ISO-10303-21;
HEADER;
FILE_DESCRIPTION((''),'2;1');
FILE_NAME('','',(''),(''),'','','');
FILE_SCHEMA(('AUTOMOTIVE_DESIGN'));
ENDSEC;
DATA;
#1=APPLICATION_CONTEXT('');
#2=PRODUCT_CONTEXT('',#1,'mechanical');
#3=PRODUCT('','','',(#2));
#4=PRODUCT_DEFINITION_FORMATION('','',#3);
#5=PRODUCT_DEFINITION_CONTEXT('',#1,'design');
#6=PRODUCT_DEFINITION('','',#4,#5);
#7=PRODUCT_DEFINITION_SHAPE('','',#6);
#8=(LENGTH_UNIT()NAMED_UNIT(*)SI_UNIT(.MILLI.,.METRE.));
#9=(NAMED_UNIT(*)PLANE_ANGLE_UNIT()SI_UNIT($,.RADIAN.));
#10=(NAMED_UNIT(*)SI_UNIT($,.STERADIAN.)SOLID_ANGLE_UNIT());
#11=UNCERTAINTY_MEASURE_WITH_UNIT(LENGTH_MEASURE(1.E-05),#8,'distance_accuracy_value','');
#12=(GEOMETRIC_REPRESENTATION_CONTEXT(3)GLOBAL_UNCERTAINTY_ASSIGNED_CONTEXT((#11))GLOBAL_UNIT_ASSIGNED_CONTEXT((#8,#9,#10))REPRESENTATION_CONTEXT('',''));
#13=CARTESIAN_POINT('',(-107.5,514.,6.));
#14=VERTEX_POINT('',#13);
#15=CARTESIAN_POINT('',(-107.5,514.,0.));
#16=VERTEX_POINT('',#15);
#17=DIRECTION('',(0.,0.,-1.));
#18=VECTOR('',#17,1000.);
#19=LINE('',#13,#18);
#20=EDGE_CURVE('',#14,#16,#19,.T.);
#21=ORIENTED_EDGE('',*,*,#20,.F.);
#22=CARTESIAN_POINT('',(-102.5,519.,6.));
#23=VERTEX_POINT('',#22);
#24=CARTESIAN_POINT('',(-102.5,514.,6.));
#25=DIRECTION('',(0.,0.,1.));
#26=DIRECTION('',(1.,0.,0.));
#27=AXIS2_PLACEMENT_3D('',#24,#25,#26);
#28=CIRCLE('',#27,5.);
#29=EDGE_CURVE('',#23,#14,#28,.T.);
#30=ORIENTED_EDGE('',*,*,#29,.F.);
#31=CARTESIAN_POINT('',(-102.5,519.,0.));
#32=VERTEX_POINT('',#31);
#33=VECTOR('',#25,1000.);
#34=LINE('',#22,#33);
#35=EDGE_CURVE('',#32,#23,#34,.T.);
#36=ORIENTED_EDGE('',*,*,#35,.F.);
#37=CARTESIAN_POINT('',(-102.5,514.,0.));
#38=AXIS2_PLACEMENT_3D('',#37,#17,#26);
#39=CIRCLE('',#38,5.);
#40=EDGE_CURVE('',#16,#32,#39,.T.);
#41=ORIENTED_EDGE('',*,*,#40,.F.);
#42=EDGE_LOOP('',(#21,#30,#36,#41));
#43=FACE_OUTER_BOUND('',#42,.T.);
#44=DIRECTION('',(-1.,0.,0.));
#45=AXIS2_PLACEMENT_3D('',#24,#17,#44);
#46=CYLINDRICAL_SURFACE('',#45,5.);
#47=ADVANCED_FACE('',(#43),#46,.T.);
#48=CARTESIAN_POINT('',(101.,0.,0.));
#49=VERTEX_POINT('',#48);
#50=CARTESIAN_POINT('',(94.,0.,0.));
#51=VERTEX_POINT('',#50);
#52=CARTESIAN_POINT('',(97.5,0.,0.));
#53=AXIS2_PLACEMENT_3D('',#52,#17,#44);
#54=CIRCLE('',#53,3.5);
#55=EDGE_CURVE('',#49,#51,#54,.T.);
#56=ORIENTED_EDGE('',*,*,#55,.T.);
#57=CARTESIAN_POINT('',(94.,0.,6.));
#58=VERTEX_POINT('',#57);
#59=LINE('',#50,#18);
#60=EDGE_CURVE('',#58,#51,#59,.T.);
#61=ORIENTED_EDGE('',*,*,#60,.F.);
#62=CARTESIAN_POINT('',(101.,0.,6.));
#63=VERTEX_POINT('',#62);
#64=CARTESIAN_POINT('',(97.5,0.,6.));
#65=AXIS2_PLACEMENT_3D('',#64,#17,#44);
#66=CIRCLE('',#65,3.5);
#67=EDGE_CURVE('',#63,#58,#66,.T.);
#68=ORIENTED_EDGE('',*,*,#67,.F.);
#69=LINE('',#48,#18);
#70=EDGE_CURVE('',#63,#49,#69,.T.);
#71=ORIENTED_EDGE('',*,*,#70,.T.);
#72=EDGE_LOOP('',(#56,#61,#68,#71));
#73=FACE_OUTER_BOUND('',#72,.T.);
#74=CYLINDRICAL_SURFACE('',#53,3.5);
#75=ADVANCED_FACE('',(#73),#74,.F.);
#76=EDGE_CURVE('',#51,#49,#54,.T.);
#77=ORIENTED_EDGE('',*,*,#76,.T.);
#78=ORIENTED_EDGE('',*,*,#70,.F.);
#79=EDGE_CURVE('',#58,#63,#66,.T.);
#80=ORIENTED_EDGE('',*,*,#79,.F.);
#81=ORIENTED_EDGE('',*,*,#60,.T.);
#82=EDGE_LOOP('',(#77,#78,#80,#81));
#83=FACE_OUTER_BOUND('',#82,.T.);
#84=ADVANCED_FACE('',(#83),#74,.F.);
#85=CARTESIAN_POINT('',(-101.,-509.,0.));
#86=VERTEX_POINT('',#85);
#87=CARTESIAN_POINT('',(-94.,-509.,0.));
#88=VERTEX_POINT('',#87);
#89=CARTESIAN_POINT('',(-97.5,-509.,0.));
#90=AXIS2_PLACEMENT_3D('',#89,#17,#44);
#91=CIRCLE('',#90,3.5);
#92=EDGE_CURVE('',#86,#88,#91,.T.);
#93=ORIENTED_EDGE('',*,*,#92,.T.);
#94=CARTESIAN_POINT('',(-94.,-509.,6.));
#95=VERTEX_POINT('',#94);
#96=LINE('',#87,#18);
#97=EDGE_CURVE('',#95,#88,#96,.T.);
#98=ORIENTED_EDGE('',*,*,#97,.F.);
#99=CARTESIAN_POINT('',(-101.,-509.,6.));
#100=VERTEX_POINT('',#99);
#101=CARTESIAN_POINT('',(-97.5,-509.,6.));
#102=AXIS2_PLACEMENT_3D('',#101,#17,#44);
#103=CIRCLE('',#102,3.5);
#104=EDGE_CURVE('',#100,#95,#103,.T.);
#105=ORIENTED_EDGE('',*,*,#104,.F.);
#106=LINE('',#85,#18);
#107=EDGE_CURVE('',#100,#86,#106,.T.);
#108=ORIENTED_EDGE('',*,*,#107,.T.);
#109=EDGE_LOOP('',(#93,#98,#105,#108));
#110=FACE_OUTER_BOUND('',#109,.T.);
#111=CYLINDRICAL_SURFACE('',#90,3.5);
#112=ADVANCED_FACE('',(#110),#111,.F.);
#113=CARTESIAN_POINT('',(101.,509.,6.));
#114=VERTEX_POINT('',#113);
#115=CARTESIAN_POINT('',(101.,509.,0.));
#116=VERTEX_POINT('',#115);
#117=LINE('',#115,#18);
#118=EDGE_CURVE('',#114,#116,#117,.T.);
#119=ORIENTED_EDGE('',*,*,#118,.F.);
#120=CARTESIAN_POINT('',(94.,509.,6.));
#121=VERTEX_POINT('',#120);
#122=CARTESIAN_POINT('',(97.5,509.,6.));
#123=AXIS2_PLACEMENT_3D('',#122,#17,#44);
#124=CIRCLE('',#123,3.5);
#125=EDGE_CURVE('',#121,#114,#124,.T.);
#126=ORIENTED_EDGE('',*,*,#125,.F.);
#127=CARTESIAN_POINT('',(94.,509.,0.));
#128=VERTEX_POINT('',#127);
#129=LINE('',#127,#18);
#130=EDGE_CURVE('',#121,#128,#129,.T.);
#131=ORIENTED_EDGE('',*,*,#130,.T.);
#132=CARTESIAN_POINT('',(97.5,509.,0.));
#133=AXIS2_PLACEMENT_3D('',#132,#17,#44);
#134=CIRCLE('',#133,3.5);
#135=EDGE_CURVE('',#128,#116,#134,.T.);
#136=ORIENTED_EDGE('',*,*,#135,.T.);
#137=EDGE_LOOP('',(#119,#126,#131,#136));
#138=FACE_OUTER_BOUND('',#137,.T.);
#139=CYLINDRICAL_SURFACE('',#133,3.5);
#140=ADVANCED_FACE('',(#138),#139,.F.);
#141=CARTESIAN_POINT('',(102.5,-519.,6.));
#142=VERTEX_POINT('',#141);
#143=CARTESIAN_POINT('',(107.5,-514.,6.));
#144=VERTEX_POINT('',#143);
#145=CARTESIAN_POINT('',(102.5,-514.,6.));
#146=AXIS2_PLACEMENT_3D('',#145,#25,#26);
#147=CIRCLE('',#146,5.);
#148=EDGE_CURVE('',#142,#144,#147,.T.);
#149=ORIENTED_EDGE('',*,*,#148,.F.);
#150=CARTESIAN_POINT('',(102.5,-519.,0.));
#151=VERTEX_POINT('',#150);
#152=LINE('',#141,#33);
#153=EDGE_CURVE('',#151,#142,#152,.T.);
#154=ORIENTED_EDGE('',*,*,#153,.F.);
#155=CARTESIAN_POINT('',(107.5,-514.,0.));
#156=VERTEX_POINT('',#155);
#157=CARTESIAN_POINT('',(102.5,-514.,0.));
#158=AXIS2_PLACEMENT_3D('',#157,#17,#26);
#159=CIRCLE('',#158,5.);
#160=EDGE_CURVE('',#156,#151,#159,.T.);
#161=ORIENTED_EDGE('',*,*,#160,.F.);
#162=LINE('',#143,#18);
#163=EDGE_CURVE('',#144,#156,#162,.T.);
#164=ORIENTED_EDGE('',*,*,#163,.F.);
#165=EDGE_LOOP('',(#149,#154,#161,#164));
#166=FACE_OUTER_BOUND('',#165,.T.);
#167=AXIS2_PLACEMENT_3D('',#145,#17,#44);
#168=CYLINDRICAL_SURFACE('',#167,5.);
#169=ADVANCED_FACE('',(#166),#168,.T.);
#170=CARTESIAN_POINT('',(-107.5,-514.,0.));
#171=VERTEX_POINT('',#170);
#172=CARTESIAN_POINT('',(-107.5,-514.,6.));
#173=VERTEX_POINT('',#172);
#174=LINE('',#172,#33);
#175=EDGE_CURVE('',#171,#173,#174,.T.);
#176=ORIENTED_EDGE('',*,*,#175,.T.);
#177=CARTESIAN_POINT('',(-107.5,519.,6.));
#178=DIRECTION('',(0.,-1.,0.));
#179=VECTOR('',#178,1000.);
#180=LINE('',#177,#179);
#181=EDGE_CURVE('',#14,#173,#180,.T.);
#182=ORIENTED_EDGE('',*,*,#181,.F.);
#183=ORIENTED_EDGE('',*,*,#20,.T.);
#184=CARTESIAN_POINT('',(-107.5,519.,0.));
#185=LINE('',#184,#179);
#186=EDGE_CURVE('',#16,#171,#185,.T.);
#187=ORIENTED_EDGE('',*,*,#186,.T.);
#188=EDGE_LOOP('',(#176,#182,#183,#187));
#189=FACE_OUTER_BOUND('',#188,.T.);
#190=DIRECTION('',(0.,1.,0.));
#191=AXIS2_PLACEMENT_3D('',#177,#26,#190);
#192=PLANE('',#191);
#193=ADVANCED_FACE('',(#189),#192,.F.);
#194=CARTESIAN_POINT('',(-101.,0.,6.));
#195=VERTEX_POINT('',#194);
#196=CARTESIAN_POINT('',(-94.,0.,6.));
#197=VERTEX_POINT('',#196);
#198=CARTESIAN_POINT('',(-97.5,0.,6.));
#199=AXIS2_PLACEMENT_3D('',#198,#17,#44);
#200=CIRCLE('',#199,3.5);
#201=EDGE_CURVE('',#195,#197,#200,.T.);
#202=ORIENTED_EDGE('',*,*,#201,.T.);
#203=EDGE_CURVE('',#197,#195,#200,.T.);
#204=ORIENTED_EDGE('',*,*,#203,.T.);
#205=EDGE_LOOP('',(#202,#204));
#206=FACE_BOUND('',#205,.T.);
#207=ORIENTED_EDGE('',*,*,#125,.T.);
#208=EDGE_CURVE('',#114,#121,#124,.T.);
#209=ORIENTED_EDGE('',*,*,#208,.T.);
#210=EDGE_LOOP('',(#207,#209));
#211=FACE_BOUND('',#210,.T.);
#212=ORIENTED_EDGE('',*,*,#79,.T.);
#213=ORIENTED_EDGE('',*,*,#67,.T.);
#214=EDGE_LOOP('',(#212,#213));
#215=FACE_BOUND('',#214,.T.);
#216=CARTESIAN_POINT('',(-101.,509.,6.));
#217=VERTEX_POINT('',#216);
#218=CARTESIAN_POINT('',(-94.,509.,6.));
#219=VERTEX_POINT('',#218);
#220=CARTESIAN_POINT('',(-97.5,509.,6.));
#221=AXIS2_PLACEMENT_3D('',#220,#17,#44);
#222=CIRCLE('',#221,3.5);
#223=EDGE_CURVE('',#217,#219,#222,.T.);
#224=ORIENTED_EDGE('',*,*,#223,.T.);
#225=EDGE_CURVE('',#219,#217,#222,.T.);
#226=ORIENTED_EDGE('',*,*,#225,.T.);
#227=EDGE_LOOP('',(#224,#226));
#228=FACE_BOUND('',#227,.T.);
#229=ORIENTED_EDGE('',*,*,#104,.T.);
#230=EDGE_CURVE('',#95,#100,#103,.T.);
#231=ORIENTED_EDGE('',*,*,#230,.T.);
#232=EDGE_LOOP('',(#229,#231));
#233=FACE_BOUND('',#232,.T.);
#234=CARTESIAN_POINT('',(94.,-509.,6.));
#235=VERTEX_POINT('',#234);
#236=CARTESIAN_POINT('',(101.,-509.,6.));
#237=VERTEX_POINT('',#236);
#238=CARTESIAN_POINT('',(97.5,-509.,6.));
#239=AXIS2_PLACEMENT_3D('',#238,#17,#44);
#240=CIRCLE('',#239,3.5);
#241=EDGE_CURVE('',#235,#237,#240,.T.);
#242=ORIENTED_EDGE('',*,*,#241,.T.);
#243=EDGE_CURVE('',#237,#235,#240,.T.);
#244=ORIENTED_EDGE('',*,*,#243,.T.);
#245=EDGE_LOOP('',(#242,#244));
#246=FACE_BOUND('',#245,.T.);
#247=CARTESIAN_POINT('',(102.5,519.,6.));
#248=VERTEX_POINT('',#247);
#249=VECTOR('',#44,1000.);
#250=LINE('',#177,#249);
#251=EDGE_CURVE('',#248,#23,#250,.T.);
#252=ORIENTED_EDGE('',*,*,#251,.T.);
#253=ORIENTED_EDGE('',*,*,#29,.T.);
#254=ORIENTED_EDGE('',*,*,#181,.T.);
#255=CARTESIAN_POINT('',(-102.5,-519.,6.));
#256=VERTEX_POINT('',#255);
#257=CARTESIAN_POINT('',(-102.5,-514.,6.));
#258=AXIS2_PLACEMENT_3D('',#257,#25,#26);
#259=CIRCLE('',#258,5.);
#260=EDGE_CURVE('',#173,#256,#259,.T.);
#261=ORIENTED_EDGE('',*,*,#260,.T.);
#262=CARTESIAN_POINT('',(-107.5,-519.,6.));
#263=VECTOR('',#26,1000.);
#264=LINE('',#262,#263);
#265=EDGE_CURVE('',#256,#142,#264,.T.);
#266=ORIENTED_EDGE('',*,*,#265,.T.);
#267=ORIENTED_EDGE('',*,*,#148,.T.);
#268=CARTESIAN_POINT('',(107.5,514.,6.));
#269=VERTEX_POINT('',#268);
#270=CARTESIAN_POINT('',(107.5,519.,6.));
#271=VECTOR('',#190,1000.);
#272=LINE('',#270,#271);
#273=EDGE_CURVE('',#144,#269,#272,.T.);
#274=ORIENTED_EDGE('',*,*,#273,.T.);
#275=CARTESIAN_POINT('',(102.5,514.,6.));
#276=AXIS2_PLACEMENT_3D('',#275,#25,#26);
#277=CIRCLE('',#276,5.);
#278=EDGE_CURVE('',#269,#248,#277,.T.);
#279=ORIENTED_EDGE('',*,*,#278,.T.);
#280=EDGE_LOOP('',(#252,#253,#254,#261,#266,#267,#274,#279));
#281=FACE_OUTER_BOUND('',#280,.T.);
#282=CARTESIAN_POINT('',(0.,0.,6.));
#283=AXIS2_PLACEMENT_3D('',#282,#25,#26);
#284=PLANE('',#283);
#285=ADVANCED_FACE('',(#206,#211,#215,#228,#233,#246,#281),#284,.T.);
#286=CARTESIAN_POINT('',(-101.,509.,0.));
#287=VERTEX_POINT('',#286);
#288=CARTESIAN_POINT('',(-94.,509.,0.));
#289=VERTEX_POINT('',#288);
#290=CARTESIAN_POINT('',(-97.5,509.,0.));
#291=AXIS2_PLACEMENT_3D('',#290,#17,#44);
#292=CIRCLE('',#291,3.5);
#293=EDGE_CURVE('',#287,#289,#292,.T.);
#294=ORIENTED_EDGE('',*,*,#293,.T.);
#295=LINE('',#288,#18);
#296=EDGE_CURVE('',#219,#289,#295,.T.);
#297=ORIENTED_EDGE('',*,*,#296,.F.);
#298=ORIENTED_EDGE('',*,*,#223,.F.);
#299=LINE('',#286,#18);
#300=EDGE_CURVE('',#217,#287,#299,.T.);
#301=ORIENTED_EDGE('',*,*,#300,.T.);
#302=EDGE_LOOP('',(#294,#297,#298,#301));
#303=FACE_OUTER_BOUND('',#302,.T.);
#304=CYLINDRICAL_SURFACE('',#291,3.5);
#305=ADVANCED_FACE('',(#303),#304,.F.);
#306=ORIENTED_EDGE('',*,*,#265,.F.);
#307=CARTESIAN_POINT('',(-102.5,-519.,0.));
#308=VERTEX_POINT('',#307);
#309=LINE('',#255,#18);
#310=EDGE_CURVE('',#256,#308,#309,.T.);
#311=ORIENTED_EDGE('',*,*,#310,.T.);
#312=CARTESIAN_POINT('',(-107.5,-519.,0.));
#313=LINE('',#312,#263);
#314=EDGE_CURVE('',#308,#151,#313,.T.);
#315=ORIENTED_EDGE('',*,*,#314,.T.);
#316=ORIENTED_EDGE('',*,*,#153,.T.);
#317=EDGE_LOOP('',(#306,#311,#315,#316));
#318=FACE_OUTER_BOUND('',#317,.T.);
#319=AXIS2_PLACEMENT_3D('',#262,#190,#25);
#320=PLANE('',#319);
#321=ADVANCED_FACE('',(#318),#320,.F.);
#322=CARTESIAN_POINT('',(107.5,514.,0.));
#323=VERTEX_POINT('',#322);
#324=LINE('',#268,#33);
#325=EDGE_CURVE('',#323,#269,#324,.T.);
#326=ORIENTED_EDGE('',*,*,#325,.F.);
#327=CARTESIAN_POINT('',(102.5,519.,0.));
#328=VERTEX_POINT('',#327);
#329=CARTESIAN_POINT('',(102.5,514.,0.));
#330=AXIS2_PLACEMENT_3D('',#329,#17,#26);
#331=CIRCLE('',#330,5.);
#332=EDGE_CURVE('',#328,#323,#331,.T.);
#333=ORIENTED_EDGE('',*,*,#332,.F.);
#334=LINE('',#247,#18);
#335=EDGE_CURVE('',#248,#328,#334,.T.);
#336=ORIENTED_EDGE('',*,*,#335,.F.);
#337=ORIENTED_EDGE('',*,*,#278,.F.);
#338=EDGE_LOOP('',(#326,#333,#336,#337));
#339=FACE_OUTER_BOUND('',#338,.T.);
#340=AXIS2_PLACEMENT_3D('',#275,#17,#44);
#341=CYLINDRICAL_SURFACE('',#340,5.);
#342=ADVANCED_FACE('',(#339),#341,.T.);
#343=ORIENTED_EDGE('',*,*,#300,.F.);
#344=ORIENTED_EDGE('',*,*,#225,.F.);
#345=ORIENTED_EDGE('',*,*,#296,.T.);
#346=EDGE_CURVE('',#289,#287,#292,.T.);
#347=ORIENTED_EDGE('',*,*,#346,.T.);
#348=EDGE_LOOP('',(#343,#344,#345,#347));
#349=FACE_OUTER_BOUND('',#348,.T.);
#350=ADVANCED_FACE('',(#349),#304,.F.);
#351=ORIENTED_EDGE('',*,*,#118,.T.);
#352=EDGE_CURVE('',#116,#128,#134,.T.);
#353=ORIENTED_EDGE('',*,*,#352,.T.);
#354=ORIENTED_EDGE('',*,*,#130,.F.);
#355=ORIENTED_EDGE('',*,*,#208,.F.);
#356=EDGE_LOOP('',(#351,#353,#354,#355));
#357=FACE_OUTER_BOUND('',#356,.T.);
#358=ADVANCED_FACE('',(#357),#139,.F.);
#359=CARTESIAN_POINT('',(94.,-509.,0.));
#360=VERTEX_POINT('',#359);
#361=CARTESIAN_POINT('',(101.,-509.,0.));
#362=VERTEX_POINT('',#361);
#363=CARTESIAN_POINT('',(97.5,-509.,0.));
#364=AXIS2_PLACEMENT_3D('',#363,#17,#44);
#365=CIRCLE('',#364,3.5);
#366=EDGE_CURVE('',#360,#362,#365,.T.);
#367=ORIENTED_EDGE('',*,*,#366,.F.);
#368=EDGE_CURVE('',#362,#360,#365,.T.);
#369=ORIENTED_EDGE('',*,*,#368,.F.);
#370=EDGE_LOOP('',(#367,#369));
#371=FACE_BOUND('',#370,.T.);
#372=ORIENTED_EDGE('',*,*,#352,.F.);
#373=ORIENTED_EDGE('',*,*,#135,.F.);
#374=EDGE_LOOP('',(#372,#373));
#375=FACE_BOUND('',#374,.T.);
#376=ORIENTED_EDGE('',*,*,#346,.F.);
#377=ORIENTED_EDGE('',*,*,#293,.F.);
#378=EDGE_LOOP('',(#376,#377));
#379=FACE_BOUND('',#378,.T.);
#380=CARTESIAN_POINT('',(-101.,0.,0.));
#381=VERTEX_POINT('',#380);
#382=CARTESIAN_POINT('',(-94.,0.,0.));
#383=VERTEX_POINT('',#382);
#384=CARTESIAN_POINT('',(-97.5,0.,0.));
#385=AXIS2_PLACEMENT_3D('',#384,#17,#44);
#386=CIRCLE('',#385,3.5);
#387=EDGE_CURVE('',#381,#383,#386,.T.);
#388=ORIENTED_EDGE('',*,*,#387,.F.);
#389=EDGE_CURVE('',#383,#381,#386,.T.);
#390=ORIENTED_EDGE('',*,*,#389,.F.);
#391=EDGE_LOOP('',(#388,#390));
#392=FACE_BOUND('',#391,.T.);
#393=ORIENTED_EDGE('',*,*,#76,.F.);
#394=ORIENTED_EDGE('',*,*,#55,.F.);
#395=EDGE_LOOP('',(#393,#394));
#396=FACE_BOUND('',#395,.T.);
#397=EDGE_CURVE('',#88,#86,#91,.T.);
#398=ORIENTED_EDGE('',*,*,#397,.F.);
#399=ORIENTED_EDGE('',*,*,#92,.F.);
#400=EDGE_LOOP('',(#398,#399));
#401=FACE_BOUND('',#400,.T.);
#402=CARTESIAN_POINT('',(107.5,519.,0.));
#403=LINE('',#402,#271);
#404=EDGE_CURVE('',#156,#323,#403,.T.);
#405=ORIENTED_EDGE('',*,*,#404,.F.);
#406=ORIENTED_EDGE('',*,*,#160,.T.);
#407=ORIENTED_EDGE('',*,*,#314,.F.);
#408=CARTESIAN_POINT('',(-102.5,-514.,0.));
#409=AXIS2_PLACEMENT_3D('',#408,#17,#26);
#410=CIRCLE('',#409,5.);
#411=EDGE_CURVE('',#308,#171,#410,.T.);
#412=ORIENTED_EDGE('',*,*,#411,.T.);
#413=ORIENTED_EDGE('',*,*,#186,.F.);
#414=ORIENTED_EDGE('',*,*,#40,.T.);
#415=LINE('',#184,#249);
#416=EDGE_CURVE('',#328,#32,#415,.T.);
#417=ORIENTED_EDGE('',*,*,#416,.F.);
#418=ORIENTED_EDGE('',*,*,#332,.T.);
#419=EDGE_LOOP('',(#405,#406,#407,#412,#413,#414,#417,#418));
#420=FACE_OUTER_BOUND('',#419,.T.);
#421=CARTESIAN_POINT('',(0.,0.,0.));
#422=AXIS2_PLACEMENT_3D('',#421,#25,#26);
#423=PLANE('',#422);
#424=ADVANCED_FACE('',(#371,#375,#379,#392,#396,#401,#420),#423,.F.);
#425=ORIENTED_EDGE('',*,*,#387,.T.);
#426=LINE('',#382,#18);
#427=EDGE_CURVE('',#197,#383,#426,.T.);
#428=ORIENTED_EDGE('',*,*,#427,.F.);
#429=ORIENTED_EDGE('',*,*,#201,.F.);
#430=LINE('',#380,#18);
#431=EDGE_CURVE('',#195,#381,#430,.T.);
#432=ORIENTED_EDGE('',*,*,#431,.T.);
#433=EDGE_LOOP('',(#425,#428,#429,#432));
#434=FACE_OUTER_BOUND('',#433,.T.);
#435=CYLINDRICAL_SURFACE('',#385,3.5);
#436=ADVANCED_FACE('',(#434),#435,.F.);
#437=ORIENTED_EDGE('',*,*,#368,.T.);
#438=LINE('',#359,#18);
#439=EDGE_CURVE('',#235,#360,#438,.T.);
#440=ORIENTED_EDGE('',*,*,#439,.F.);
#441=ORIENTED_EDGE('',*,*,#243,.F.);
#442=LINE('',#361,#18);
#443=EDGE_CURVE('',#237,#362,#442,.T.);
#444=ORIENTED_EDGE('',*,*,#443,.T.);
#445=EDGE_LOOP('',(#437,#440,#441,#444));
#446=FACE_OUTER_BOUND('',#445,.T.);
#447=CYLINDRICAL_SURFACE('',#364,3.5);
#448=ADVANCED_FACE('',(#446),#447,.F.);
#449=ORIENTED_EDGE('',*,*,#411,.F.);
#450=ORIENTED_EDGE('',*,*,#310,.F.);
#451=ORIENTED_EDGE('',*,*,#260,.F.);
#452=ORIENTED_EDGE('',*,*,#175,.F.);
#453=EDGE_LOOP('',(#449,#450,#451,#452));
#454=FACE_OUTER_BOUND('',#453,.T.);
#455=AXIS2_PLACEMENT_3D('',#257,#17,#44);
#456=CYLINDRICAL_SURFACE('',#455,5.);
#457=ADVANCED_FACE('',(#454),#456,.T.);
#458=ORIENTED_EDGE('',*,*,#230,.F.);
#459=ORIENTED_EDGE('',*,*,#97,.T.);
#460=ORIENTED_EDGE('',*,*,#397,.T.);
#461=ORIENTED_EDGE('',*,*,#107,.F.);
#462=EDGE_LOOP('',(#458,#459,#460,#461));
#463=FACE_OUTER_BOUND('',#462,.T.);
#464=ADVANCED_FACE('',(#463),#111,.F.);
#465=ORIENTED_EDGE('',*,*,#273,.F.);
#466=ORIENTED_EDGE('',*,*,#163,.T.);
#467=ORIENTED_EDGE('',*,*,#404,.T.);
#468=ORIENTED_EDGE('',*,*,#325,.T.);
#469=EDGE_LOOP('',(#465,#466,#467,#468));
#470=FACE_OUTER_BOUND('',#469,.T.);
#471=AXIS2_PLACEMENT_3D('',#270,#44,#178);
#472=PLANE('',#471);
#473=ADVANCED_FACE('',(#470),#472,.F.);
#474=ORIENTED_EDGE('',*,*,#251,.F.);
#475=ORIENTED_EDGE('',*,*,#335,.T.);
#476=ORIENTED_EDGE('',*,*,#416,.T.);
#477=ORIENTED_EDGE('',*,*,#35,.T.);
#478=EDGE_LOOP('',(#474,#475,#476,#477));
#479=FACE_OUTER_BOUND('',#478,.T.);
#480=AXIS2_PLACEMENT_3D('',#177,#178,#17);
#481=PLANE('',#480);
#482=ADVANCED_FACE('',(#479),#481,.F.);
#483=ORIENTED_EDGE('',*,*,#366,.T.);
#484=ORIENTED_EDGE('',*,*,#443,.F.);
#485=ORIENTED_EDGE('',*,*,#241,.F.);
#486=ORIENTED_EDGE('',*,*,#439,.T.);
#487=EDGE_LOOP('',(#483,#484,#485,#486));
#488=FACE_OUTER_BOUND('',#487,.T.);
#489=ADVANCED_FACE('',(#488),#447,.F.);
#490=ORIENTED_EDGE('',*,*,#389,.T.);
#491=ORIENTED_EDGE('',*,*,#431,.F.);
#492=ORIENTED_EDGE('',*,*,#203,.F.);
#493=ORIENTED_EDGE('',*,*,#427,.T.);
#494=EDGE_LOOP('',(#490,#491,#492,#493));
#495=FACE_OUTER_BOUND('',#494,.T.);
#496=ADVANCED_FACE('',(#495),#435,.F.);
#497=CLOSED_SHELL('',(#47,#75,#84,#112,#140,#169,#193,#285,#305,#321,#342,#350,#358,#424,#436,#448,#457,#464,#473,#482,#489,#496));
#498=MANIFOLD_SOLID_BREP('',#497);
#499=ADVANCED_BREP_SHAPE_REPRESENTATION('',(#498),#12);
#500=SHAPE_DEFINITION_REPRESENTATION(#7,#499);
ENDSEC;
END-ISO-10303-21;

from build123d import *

# Parameters (mm, degrees)
SKETCH_1_W            = 215
SKETCH_1_H            = 1038
EXTRUDE_1_DEPTH       = 6
HOLE_WIZARD_7_0_7_1_D = 7
FILLET_1_R            = 5


with BuildPart() as part:
    # 草图1 → 凸台-拉伸1 (new body)
    with BuildSketch(Plane.XY):
        Rectangle(SKETCH_1_W, SKETCH_1_H)
    extrude(amount=EXTRUDE_1_DEPTH)

    # Ø7.0 (7) 直径孔1 (through all)
    with Locations(Plane(origin=(0, 0, 0), x_dir=(-1, 0, 0), z_dir=(0, 0, -1))):
        with Locations((-97.5, 509), (-97.5, -509), (97.5, 509), (97.5, -509), (-97.5, 0), (97.5, 0)):
            Hole(HOLE_WIZARD_7_0_7_1_D / 2)

    # 圆角1
    fillet_1_edges = [part.edges().sort_by_distance(p)[0] for p in [
        (107.5, -519, 3),
        (-107.5, -519, 3),
        (-107.5, 519, 3),
        (107.5, 519, 3),
    ]]
    fillet(fillet_1_edges, radius=FILLET_1_R)


solid = part.part
